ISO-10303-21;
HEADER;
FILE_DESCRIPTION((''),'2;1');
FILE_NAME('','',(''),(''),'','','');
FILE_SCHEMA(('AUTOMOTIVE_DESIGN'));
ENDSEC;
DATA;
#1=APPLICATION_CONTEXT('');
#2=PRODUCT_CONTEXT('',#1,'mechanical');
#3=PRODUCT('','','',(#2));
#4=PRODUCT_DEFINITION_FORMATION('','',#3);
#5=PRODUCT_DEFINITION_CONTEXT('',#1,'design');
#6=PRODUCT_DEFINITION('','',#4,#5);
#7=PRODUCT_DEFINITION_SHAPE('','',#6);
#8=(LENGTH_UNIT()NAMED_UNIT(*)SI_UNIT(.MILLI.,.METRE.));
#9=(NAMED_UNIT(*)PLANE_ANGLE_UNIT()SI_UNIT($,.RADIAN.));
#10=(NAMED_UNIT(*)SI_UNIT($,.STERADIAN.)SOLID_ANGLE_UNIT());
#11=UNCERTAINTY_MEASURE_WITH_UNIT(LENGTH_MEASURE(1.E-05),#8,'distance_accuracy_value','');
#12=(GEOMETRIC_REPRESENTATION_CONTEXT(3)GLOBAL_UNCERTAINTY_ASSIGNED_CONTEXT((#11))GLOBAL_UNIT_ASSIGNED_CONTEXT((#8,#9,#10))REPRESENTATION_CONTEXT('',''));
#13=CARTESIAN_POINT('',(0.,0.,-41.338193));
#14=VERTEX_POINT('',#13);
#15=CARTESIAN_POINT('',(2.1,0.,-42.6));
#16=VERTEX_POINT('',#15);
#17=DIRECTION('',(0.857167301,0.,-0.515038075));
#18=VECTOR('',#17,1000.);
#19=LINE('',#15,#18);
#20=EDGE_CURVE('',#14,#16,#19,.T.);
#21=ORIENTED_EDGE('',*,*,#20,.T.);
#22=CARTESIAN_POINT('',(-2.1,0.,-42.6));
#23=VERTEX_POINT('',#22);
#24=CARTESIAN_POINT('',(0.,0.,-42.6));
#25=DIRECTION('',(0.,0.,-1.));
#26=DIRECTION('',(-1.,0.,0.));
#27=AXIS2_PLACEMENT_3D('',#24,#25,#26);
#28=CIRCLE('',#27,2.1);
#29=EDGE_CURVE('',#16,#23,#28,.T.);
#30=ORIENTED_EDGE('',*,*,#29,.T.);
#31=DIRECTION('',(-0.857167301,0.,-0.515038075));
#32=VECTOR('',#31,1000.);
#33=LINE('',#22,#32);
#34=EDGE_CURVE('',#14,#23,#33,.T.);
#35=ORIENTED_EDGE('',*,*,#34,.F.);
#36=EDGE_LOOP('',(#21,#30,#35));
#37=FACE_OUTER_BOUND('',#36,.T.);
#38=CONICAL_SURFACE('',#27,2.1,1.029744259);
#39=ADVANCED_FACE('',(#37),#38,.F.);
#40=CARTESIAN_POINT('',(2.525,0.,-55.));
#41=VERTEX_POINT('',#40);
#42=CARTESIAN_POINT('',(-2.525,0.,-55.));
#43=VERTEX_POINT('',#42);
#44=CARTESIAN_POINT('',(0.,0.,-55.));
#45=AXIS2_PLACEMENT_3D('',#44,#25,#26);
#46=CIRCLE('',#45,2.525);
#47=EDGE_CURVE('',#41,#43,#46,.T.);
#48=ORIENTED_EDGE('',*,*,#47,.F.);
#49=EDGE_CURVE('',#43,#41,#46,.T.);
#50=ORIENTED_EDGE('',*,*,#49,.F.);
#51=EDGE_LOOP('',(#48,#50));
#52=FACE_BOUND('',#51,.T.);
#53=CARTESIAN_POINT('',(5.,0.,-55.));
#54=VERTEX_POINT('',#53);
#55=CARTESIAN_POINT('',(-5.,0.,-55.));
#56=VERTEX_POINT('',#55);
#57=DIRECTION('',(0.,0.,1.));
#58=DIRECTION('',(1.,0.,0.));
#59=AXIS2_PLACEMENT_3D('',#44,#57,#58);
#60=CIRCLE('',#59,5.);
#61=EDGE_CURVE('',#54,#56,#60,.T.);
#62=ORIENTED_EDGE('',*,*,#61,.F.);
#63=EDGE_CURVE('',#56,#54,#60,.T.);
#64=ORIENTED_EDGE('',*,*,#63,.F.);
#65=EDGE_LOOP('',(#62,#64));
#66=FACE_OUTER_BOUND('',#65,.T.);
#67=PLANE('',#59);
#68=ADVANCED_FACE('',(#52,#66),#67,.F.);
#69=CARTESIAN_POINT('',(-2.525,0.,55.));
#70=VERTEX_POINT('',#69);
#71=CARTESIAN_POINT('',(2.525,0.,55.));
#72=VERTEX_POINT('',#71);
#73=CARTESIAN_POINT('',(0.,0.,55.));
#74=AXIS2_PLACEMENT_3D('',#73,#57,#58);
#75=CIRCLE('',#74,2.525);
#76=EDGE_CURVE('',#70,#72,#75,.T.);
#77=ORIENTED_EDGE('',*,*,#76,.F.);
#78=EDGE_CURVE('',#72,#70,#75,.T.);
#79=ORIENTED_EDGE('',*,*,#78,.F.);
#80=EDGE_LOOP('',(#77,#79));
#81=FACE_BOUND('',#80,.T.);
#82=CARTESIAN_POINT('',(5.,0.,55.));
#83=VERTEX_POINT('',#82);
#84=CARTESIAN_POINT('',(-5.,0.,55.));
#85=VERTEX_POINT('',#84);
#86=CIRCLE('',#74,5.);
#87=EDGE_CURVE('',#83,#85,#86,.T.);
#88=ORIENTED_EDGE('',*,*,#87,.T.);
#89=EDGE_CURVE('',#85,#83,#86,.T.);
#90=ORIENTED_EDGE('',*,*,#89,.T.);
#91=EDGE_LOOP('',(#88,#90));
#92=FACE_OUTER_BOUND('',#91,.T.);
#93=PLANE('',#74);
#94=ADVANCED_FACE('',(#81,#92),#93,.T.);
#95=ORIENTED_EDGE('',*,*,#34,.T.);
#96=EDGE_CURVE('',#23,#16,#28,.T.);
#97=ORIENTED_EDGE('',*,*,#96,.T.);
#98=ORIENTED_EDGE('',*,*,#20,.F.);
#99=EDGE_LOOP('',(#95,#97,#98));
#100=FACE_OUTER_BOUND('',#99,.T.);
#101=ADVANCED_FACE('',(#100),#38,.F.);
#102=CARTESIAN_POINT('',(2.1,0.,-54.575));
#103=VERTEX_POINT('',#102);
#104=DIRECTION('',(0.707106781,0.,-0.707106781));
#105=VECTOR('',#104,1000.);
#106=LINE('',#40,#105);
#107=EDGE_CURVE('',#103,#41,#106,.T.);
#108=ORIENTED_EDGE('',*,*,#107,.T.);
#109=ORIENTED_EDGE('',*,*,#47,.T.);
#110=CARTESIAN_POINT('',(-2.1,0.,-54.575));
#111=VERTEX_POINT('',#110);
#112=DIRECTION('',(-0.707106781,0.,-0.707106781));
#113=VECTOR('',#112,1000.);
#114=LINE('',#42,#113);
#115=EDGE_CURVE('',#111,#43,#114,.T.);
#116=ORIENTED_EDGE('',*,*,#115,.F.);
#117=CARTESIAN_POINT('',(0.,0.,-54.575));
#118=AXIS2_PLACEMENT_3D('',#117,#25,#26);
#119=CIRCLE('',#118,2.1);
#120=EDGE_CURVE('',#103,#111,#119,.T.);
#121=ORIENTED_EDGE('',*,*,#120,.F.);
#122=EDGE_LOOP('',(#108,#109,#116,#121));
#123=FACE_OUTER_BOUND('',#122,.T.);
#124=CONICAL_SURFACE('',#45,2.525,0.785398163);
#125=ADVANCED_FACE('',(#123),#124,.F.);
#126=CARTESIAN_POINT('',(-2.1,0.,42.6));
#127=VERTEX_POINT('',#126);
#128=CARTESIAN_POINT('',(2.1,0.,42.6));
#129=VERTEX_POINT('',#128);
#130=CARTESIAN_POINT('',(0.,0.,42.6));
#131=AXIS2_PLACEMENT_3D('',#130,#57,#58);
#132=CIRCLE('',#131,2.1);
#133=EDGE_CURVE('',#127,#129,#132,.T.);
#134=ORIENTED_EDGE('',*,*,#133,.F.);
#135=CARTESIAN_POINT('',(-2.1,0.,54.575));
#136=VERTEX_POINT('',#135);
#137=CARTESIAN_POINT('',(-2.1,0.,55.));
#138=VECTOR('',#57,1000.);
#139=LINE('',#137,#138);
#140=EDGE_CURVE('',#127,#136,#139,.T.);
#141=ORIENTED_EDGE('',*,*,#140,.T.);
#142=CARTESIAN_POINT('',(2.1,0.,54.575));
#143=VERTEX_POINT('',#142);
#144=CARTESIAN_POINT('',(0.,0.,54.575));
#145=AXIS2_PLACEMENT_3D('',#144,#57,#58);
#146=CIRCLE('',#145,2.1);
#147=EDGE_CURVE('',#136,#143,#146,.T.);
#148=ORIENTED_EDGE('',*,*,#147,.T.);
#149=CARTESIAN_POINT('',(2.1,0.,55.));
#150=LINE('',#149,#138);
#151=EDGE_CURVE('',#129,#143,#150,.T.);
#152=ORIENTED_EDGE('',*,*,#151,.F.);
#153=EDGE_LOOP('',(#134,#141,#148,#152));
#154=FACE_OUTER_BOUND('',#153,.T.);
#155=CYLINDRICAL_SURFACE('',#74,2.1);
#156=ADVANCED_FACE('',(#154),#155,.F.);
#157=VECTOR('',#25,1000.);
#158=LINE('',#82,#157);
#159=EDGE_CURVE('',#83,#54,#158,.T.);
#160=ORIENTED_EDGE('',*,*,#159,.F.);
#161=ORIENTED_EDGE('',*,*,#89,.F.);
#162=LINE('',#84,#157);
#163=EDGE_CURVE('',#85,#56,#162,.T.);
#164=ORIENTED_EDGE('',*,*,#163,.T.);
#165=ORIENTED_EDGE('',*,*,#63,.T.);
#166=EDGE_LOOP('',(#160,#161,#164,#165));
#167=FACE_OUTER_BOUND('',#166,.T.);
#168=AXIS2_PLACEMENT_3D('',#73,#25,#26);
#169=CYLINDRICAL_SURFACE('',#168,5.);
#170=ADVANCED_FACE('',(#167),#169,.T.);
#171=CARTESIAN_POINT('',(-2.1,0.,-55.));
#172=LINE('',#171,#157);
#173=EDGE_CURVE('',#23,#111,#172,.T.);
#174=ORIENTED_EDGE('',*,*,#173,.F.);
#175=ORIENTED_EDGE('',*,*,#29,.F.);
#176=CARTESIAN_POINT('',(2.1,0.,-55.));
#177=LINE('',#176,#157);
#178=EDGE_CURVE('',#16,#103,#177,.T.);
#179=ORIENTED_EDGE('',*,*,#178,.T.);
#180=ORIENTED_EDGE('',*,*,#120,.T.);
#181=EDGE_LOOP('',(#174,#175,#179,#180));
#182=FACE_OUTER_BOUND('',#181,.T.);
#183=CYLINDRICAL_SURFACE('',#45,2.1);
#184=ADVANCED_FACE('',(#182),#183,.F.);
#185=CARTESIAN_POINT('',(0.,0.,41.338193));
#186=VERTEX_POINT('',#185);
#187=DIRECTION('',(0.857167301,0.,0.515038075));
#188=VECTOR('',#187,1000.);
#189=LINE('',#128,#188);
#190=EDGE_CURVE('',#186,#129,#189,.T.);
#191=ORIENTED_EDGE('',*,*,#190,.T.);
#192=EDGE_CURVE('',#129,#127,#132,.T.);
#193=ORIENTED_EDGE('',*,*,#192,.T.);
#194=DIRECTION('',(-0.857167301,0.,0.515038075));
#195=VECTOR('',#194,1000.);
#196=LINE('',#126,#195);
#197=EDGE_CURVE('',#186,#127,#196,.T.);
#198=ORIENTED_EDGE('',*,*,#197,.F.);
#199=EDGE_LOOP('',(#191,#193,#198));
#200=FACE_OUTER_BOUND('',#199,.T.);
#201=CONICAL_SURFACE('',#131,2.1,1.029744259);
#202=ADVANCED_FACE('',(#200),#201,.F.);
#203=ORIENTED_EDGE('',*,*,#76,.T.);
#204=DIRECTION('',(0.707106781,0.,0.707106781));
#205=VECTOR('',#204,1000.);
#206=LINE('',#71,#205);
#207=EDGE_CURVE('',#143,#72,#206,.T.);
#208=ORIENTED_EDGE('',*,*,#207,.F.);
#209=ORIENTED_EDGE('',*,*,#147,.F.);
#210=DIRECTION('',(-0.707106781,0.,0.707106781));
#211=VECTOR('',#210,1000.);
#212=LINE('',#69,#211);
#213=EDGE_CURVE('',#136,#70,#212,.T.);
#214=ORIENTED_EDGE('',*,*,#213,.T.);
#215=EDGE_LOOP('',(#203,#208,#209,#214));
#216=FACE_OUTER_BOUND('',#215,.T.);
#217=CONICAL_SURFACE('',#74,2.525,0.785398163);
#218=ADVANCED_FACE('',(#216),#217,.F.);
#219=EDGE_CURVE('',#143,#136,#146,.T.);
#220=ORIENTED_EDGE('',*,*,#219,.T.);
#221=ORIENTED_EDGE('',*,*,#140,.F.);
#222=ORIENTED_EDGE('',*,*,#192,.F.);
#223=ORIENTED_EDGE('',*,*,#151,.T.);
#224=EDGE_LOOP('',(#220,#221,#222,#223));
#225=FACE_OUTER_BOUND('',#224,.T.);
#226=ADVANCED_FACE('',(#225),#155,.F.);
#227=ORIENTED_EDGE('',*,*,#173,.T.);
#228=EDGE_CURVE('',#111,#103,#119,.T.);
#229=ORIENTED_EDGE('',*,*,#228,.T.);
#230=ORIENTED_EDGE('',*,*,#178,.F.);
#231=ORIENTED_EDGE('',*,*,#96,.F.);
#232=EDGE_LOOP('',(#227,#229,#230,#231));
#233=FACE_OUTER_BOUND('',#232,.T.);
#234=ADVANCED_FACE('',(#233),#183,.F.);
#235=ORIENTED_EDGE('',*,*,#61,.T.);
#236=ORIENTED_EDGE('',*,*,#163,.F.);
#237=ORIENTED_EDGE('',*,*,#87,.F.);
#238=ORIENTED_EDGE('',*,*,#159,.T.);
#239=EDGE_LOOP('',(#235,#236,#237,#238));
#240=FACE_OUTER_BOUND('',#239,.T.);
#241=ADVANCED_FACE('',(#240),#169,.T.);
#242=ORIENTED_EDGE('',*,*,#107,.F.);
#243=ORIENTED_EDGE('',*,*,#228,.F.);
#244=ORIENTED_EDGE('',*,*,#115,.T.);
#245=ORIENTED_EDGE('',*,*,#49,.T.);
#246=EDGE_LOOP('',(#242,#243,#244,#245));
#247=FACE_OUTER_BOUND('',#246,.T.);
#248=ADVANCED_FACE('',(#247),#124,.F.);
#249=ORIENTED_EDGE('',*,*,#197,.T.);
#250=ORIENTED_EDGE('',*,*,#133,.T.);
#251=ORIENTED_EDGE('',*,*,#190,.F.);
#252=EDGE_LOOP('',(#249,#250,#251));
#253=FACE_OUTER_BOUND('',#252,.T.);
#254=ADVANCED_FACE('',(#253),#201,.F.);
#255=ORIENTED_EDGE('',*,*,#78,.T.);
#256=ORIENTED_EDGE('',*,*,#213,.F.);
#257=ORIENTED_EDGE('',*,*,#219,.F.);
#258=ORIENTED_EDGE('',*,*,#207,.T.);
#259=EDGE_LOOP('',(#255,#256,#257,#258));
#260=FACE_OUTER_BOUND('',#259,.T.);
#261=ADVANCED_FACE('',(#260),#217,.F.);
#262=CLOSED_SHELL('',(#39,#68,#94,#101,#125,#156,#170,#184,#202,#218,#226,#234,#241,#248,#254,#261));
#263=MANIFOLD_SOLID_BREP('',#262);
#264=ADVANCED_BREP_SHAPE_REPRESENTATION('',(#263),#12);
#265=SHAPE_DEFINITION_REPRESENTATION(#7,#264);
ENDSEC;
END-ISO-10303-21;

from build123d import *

# Parameters (mm, degrees)
SKETCH_1_R      = 5
EXTRUDE_1_DEPTH = 55


with BuildPart() as part:
    # 草图1 → 凸台-拉伸1 (new, symmetric)
    with BuildSketch(Plane.XY):
        Circle(SKETCH_1_R)
    extrude(amount=EXTRUDE_1_DEPTH, both=True)

    # 草图3 → M5x0.8 螺纹孔1 (revolve, cut)
    with BuildSketch(Plane(origin=(0, 0, 55), x_dir=(0, -1, 0), z_dir=(1, 0, 0))):
        Polygon((0, 0), (0, 13.6618073), (2.1, 12.4), (2.1, 0.425), (2.525, 0), align=None)
    m5x0_8_1 = revolve(axis=Axis((0, 0, 61.35), (0, 0, -1)), mode=Mode.SUBTRACT)

    # 镜向1: M5x0.8 螺纹孔1 across plane
    add(m5x0_8_1.mirror(Plane.XY), mode=Mode.SUBTRACT)


solid = part.part
